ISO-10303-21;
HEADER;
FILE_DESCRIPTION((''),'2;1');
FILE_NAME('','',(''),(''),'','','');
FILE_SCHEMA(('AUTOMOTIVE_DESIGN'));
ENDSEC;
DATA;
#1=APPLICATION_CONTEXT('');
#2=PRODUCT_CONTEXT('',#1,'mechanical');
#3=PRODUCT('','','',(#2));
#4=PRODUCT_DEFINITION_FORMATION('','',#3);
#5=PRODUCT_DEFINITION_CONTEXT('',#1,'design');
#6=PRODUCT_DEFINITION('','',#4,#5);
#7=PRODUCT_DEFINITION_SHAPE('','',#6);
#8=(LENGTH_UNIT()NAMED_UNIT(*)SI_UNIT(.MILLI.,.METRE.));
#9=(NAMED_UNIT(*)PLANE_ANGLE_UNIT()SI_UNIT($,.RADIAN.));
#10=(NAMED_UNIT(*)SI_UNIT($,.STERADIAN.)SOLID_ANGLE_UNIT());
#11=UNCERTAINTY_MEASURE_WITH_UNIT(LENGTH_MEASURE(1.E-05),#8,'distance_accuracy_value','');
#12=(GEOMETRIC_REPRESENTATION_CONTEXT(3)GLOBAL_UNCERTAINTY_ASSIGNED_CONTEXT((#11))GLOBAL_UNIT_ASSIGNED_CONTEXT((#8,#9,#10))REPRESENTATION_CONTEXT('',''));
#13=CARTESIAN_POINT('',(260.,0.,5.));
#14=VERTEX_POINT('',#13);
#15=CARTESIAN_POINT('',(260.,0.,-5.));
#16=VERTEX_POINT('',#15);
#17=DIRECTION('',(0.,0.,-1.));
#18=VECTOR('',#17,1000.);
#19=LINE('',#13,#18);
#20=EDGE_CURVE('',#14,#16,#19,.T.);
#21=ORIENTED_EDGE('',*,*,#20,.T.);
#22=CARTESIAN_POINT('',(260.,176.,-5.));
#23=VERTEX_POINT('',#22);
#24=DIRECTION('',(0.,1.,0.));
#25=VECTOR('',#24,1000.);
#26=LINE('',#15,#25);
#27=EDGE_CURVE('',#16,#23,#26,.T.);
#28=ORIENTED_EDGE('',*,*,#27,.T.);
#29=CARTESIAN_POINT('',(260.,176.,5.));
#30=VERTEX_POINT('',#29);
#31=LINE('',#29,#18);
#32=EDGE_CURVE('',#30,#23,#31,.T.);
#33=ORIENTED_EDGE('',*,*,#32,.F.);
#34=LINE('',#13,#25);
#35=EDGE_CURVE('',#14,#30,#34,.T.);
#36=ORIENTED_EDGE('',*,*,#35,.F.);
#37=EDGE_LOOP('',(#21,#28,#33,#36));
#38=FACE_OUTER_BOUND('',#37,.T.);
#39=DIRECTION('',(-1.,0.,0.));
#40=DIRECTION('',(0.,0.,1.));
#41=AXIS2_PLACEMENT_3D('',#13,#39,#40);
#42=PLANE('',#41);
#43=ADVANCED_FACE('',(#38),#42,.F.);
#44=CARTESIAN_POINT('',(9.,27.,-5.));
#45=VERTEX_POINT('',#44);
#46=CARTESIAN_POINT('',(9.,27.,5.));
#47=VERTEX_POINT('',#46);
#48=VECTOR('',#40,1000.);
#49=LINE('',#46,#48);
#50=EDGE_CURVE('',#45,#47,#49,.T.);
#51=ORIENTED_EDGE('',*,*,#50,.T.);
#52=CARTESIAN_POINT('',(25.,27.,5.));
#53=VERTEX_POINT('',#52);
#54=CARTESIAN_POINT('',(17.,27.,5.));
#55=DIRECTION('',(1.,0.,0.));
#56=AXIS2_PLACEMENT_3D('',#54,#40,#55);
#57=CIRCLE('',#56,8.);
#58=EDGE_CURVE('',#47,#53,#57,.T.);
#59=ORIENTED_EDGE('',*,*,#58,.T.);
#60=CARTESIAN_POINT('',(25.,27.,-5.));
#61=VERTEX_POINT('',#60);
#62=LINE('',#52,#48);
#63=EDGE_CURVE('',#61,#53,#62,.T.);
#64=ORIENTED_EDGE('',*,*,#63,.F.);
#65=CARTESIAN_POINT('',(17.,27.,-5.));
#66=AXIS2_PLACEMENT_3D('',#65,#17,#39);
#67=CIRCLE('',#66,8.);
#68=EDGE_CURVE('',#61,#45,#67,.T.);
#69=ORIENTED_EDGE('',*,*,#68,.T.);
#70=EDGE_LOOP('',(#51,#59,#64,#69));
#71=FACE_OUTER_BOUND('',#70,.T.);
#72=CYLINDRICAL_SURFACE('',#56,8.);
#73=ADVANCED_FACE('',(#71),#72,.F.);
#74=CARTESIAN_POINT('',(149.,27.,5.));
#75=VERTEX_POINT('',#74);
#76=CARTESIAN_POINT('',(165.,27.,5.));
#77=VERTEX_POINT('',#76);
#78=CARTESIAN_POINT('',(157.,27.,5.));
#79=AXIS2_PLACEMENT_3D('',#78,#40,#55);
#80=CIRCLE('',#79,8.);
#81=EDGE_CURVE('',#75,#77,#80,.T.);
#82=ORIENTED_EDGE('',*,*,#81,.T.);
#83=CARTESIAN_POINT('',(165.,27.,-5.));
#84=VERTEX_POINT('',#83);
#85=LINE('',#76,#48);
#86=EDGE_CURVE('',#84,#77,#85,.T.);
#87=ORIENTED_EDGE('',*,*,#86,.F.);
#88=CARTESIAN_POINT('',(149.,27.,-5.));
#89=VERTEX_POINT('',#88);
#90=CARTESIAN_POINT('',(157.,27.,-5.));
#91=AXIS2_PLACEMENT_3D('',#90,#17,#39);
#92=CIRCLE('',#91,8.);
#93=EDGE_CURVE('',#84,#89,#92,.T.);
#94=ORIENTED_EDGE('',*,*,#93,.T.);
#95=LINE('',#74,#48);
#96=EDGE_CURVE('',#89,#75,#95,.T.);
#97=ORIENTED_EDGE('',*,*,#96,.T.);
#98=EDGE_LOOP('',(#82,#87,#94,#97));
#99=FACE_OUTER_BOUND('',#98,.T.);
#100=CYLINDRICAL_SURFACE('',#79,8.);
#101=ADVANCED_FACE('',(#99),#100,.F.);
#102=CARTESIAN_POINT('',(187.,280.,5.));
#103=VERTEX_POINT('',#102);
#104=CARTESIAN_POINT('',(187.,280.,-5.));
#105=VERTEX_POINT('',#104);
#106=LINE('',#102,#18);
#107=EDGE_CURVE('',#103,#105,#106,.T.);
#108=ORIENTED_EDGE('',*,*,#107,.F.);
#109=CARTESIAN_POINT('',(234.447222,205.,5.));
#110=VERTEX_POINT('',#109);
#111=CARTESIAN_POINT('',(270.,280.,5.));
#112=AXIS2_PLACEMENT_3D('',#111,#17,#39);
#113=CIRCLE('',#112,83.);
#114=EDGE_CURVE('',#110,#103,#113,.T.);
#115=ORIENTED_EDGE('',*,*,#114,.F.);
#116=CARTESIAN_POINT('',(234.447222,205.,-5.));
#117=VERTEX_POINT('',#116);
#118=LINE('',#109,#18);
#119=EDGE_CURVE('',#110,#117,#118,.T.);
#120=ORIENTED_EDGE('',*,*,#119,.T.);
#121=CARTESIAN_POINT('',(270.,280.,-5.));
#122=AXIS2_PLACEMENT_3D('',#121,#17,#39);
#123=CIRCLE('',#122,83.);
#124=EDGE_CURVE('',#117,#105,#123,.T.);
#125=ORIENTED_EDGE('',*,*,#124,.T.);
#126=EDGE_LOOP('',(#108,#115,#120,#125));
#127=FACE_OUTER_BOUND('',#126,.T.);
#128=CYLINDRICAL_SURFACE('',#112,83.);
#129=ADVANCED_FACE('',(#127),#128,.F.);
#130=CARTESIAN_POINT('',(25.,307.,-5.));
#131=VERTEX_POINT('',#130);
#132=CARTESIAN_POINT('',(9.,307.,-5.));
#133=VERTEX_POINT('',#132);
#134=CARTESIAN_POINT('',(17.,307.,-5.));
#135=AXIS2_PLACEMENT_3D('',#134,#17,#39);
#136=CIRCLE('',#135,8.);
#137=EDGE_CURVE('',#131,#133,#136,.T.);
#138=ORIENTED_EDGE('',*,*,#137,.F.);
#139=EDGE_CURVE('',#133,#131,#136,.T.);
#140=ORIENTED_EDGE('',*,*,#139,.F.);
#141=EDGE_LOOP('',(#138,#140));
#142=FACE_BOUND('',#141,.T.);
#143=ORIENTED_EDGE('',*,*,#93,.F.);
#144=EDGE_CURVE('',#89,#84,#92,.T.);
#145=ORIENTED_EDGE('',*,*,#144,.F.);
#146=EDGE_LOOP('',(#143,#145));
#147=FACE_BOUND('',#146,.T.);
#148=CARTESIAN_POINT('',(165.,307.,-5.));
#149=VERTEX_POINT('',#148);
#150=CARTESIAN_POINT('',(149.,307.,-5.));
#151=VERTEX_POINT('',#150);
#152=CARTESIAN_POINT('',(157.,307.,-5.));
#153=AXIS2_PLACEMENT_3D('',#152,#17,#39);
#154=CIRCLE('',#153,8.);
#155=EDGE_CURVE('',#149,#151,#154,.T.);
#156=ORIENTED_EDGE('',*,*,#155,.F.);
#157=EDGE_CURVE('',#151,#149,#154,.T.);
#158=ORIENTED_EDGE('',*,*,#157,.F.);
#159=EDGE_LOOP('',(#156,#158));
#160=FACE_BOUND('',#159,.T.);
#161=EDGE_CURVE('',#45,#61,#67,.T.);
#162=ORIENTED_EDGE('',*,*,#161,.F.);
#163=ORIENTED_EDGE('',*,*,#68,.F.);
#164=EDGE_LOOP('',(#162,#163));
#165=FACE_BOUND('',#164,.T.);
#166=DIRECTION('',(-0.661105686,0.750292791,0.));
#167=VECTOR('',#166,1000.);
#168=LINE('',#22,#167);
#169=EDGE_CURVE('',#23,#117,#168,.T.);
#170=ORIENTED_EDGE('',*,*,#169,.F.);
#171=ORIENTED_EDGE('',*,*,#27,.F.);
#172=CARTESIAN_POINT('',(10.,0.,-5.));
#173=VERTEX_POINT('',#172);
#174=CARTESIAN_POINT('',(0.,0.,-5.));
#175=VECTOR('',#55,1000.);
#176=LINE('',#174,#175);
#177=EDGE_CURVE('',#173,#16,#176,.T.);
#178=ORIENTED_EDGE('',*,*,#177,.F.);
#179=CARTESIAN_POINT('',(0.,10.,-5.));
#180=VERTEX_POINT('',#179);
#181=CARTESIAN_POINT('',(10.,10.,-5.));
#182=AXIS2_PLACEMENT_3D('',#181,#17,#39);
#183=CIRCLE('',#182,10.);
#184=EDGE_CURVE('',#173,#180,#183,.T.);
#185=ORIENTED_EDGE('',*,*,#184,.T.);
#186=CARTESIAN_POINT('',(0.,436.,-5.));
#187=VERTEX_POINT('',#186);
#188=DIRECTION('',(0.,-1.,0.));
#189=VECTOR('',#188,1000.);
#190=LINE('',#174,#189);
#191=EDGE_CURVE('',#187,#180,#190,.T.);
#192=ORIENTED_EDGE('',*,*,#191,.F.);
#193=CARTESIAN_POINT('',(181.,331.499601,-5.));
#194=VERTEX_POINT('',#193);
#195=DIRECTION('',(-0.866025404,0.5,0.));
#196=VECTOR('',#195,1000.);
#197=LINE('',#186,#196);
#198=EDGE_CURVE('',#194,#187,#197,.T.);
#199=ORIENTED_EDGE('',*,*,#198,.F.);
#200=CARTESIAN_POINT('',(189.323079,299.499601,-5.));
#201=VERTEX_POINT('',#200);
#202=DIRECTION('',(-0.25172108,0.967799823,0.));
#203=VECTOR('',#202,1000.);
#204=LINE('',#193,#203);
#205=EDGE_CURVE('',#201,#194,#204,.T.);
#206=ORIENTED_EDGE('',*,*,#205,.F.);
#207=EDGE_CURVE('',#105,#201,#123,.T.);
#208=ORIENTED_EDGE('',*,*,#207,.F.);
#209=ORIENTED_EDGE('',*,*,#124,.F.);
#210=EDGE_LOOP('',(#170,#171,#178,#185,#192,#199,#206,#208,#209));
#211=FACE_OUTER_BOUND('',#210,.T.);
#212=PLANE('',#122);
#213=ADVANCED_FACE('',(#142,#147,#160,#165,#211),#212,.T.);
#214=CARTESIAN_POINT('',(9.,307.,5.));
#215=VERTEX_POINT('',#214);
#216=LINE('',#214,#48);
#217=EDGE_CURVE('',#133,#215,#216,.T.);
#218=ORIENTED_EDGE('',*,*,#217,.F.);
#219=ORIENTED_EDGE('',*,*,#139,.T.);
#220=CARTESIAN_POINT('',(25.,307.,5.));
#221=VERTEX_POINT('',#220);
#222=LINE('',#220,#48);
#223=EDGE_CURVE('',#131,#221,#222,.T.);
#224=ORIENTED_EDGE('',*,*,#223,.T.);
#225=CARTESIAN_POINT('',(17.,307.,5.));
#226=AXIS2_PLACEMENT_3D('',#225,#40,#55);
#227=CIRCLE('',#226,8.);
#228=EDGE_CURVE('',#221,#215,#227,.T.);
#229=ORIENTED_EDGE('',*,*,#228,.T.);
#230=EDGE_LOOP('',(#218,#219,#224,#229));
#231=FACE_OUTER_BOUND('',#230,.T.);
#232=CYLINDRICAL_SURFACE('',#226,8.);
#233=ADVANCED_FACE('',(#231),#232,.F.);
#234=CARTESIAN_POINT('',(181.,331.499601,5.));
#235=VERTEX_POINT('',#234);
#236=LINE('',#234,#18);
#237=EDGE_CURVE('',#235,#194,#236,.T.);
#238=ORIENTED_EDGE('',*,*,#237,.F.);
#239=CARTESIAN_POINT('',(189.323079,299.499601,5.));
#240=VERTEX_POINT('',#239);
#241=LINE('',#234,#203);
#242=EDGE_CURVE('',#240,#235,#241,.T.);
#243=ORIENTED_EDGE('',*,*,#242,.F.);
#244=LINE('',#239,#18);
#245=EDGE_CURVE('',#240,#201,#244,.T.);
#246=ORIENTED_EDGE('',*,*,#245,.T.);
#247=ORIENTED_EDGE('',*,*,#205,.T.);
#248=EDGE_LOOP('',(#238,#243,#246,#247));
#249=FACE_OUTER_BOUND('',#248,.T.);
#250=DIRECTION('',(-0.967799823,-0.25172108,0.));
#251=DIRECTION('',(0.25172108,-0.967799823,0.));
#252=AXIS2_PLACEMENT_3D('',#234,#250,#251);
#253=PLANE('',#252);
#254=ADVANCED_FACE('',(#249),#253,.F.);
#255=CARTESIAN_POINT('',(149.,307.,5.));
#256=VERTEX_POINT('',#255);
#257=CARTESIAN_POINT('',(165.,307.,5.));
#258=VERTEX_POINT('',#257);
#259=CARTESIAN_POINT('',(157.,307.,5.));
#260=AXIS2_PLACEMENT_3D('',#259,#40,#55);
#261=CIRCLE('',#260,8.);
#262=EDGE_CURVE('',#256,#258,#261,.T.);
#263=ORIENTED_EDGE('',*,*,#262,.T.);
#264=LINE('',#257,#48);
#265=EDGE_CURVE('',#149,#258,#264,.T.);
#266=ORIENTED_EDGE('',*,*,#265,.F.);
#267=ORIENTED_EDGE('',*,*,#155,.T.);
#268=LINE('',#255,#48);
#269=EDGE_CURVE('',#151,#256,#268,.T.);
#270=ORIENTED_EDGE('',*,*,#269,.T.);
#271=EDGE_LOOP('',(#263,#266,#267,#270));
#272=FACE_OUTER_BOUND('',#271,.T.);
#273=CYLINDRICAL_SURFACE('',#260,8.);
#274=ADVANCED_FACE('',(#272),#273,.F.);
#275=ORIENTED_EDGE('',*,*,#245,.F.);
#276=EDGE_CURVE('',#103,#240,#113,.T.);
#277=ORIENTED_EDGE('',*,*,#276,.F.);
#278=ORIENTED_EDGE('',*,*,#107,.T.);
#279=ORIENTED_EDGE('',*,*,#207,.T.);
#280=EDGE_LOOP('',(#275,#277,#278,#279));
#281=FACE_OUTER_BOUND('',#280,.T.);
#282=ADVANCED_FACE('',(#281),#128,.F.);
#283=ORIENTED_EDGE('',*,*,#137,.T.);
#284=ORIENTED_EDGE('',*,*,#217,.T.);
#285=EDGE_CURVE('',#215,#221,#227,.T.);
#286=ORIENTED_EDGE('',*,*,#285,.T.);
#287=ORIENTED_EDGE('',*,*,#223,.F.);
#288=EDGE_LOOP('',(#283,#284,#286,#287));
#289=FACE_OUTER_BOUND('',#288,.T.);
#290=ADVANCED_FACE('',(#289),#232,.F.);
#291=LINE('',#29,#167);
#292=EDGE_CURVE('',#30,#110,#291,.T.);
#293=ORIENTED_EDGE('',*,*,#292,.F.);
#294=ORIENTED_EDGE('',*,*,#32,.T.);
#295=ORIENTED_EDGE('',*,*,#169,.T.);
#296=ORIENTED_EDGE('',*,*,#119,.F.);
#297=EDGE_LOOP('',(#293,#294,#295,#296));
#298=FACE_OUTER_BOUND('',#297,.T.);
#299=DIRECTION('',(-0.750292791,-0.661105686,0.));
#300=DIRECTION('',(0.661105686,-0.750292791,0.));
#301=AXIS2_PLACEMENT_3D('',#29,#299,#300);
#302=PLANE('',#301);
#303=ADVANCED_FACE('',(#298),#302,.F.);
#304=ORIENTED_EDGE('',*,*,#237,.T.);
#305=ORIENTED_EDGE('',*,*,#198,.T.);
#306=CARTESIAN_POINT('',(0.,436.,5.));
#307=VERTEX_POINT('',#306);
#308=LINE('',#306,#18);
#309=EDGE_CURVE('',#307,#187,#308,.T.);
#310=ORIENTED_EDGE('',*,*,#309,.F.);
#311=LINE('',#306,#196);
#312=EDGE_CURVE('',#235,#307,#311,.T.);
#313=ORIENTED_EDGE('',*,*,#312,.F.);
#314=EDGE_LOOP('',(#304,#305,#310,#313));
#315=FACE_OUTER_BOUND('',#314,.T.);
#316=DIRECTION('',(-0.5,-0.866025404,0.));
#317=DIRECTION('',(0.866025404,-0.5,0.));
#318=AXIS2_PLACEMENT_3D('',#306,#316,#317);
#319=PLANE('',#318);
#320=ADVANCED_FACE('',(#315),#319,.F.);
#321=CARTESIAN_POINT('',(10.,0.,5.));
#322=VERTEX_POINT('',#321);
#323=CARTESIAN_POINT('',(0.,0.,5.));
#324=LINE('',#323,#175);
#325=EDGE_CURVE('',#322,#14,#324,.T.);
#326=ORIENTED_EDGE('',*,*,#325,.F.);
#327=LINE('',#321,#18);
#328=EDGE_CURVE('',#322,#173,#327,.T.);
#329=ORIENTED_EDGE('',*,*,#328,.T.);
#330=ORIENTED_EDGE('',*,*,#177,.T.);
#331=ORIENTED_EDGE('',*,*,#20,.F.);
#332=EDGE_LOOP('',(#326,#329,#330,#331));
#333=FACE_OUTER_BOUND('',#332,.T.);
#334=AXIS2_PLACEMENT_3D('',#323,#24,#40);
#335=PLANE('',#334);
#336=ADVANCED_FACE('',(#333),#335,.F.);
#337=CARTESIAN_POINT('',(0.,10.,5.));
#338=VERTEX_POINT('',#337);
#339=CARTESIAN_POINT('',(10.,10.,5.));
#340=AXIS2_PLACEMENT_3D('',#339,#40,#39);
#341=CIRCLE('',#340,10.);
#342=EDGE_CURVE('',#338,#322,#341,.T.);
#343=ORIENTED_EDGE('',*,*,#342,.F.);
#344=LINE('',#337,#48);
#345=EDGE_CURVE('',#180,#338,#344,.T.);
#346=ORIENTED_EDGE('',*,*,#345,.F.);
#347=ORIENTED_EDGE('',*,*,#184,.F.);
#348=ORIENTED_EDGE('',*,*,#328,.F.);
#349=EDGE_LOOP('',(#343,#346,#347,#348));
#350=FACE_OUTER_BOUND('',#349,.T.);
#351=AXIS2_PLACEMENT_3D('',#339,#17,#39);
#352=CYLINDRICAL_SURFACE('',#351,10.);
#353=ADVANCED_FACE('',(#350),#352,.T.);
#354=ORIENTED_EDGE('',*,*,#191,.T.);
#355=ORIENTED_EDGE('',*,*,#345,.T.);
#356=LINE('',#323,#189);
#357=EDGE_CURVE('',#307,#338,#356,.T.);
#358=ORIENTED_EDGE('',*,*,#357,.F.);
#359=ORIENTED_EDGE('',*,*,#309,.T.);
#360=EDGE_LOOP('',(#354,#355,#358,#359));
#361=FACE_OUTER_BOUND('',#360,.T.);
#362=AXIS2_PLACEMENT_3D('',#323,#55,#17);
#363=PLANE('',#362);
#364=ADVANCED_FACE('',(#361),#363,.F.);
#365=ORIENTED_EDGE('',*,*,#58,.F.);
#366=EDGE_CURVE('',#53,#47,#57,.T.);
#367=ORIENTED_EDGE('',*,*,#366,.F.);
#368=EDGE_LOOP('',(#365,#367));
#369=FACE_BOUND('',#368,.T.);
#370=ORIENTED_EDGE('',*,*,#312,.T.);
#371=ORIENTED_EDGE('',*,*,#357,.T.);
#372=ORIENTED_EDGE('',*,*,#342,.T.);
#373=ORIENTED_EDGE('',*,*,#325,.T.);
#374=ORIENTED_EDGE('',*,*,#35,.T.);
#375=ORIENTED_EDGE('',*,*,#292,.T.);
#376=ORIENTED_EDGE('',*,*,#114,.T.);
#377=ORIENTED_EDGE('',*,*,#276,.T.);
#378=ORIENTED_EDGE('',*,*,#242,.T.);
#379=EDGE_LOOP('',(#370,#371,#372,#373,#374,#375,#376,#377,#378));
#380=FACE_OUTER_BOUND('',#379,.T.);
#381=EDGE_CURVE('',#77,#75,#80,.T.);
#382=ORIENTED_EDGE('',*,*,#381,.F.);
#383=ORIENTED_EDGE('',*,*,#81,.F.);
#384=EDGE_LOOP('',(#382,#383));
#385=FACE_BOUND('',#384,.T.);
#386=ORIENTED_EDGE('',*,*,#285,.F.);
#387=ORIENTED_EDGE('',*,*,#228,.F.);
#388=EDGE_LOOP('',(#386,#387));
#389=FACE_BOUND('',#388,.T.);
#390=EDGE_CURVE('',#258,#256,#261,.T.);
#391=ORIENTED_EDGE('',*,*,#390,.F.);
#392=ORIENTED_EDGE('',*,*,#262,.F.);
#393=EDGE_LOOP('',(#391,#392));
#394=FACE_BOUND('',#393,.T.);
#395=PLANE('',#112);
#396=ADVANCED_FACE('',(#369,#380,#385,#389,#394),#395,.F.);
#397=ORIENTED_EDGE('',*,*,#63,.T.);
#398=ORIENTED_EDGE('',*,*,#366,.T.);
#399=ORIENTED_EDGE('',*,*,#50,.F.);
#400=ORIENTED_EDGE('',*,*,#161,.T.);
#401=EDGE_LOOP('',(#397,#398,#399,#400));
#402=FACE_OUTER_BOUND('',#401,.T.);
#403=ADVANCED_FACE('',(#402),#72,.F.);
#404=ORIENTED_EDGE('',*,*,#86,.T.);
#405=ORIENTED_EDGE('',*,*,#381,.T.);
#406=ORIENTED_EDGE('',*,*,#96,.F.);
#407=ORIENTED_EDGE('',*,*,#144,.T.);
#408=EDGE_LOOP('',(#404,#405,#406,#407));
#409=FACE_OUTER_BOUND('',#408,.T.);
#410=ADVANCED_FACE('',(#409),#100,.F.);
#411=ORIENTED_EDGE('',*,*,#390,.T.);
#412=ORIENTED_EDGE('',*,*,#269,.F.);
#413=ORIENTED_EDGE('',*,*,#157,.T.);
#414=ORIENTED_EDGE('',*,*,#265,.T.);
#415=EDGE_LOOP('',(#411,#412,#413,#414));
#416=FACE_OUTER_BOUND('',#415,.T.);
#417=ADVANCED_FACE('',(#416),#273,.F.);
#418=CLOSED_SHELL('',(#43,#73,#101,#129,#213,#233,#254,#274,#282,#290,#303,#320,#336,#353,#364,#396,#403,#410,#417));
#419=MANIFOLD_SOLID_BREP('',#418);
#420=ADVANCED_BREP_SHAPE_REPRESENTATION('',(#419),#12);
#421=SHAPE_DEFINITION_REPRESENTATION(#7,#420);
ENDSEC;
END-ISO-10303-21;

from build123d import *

# Parameters (mm, degrees)
BOSS_EXTRUDE1_DEPTH        = 5
F_16_0_16_DIAMETER_HOLE1_D = 16
FILLET1_R                  = 10


with BuildPart() as part:
    # Sketch1 → Boss-Extrude1 (new, symmetric)
    with BuildSketch(Plane.XY):
        with BuildLine():
            Line((0, 0), (0, 436))
            Line((0, 436), (181, 331.499601277))
            Line((181, 331.499601277), (189.323079198, 299.499601277))
            ThreePointArc((189.323079198, 299.499601277), (195.100872088, 244.235203929), (234.447222331, 205))
            Line((234.447222331, 205), (260, 176))
            Line((260, 176), (260, 0))
            Line((260, 0), (0, 0))
        make_face()
    extrude(amount=BOSS_EXTRUDE1_DEPTH, both=True)

    # Ø16.0 (16) Diameter Hole1 (through all)
    with Locations(Plane.XY.offset(5)):
        with Locations((17, 27), (157, 27), (157, 307), (17, 307)):
            Hole(F_16_0_16_DIAMETER_HOLE1_D / 2)

    # Fillet1
    fillet1_edges = [part.edges().sort_by_distance(p)[0] for p in [
        (0, 0, 0),
    ]]
    fillet(fillet1_edges, radius=FILLET1_R)


solid = part.part
